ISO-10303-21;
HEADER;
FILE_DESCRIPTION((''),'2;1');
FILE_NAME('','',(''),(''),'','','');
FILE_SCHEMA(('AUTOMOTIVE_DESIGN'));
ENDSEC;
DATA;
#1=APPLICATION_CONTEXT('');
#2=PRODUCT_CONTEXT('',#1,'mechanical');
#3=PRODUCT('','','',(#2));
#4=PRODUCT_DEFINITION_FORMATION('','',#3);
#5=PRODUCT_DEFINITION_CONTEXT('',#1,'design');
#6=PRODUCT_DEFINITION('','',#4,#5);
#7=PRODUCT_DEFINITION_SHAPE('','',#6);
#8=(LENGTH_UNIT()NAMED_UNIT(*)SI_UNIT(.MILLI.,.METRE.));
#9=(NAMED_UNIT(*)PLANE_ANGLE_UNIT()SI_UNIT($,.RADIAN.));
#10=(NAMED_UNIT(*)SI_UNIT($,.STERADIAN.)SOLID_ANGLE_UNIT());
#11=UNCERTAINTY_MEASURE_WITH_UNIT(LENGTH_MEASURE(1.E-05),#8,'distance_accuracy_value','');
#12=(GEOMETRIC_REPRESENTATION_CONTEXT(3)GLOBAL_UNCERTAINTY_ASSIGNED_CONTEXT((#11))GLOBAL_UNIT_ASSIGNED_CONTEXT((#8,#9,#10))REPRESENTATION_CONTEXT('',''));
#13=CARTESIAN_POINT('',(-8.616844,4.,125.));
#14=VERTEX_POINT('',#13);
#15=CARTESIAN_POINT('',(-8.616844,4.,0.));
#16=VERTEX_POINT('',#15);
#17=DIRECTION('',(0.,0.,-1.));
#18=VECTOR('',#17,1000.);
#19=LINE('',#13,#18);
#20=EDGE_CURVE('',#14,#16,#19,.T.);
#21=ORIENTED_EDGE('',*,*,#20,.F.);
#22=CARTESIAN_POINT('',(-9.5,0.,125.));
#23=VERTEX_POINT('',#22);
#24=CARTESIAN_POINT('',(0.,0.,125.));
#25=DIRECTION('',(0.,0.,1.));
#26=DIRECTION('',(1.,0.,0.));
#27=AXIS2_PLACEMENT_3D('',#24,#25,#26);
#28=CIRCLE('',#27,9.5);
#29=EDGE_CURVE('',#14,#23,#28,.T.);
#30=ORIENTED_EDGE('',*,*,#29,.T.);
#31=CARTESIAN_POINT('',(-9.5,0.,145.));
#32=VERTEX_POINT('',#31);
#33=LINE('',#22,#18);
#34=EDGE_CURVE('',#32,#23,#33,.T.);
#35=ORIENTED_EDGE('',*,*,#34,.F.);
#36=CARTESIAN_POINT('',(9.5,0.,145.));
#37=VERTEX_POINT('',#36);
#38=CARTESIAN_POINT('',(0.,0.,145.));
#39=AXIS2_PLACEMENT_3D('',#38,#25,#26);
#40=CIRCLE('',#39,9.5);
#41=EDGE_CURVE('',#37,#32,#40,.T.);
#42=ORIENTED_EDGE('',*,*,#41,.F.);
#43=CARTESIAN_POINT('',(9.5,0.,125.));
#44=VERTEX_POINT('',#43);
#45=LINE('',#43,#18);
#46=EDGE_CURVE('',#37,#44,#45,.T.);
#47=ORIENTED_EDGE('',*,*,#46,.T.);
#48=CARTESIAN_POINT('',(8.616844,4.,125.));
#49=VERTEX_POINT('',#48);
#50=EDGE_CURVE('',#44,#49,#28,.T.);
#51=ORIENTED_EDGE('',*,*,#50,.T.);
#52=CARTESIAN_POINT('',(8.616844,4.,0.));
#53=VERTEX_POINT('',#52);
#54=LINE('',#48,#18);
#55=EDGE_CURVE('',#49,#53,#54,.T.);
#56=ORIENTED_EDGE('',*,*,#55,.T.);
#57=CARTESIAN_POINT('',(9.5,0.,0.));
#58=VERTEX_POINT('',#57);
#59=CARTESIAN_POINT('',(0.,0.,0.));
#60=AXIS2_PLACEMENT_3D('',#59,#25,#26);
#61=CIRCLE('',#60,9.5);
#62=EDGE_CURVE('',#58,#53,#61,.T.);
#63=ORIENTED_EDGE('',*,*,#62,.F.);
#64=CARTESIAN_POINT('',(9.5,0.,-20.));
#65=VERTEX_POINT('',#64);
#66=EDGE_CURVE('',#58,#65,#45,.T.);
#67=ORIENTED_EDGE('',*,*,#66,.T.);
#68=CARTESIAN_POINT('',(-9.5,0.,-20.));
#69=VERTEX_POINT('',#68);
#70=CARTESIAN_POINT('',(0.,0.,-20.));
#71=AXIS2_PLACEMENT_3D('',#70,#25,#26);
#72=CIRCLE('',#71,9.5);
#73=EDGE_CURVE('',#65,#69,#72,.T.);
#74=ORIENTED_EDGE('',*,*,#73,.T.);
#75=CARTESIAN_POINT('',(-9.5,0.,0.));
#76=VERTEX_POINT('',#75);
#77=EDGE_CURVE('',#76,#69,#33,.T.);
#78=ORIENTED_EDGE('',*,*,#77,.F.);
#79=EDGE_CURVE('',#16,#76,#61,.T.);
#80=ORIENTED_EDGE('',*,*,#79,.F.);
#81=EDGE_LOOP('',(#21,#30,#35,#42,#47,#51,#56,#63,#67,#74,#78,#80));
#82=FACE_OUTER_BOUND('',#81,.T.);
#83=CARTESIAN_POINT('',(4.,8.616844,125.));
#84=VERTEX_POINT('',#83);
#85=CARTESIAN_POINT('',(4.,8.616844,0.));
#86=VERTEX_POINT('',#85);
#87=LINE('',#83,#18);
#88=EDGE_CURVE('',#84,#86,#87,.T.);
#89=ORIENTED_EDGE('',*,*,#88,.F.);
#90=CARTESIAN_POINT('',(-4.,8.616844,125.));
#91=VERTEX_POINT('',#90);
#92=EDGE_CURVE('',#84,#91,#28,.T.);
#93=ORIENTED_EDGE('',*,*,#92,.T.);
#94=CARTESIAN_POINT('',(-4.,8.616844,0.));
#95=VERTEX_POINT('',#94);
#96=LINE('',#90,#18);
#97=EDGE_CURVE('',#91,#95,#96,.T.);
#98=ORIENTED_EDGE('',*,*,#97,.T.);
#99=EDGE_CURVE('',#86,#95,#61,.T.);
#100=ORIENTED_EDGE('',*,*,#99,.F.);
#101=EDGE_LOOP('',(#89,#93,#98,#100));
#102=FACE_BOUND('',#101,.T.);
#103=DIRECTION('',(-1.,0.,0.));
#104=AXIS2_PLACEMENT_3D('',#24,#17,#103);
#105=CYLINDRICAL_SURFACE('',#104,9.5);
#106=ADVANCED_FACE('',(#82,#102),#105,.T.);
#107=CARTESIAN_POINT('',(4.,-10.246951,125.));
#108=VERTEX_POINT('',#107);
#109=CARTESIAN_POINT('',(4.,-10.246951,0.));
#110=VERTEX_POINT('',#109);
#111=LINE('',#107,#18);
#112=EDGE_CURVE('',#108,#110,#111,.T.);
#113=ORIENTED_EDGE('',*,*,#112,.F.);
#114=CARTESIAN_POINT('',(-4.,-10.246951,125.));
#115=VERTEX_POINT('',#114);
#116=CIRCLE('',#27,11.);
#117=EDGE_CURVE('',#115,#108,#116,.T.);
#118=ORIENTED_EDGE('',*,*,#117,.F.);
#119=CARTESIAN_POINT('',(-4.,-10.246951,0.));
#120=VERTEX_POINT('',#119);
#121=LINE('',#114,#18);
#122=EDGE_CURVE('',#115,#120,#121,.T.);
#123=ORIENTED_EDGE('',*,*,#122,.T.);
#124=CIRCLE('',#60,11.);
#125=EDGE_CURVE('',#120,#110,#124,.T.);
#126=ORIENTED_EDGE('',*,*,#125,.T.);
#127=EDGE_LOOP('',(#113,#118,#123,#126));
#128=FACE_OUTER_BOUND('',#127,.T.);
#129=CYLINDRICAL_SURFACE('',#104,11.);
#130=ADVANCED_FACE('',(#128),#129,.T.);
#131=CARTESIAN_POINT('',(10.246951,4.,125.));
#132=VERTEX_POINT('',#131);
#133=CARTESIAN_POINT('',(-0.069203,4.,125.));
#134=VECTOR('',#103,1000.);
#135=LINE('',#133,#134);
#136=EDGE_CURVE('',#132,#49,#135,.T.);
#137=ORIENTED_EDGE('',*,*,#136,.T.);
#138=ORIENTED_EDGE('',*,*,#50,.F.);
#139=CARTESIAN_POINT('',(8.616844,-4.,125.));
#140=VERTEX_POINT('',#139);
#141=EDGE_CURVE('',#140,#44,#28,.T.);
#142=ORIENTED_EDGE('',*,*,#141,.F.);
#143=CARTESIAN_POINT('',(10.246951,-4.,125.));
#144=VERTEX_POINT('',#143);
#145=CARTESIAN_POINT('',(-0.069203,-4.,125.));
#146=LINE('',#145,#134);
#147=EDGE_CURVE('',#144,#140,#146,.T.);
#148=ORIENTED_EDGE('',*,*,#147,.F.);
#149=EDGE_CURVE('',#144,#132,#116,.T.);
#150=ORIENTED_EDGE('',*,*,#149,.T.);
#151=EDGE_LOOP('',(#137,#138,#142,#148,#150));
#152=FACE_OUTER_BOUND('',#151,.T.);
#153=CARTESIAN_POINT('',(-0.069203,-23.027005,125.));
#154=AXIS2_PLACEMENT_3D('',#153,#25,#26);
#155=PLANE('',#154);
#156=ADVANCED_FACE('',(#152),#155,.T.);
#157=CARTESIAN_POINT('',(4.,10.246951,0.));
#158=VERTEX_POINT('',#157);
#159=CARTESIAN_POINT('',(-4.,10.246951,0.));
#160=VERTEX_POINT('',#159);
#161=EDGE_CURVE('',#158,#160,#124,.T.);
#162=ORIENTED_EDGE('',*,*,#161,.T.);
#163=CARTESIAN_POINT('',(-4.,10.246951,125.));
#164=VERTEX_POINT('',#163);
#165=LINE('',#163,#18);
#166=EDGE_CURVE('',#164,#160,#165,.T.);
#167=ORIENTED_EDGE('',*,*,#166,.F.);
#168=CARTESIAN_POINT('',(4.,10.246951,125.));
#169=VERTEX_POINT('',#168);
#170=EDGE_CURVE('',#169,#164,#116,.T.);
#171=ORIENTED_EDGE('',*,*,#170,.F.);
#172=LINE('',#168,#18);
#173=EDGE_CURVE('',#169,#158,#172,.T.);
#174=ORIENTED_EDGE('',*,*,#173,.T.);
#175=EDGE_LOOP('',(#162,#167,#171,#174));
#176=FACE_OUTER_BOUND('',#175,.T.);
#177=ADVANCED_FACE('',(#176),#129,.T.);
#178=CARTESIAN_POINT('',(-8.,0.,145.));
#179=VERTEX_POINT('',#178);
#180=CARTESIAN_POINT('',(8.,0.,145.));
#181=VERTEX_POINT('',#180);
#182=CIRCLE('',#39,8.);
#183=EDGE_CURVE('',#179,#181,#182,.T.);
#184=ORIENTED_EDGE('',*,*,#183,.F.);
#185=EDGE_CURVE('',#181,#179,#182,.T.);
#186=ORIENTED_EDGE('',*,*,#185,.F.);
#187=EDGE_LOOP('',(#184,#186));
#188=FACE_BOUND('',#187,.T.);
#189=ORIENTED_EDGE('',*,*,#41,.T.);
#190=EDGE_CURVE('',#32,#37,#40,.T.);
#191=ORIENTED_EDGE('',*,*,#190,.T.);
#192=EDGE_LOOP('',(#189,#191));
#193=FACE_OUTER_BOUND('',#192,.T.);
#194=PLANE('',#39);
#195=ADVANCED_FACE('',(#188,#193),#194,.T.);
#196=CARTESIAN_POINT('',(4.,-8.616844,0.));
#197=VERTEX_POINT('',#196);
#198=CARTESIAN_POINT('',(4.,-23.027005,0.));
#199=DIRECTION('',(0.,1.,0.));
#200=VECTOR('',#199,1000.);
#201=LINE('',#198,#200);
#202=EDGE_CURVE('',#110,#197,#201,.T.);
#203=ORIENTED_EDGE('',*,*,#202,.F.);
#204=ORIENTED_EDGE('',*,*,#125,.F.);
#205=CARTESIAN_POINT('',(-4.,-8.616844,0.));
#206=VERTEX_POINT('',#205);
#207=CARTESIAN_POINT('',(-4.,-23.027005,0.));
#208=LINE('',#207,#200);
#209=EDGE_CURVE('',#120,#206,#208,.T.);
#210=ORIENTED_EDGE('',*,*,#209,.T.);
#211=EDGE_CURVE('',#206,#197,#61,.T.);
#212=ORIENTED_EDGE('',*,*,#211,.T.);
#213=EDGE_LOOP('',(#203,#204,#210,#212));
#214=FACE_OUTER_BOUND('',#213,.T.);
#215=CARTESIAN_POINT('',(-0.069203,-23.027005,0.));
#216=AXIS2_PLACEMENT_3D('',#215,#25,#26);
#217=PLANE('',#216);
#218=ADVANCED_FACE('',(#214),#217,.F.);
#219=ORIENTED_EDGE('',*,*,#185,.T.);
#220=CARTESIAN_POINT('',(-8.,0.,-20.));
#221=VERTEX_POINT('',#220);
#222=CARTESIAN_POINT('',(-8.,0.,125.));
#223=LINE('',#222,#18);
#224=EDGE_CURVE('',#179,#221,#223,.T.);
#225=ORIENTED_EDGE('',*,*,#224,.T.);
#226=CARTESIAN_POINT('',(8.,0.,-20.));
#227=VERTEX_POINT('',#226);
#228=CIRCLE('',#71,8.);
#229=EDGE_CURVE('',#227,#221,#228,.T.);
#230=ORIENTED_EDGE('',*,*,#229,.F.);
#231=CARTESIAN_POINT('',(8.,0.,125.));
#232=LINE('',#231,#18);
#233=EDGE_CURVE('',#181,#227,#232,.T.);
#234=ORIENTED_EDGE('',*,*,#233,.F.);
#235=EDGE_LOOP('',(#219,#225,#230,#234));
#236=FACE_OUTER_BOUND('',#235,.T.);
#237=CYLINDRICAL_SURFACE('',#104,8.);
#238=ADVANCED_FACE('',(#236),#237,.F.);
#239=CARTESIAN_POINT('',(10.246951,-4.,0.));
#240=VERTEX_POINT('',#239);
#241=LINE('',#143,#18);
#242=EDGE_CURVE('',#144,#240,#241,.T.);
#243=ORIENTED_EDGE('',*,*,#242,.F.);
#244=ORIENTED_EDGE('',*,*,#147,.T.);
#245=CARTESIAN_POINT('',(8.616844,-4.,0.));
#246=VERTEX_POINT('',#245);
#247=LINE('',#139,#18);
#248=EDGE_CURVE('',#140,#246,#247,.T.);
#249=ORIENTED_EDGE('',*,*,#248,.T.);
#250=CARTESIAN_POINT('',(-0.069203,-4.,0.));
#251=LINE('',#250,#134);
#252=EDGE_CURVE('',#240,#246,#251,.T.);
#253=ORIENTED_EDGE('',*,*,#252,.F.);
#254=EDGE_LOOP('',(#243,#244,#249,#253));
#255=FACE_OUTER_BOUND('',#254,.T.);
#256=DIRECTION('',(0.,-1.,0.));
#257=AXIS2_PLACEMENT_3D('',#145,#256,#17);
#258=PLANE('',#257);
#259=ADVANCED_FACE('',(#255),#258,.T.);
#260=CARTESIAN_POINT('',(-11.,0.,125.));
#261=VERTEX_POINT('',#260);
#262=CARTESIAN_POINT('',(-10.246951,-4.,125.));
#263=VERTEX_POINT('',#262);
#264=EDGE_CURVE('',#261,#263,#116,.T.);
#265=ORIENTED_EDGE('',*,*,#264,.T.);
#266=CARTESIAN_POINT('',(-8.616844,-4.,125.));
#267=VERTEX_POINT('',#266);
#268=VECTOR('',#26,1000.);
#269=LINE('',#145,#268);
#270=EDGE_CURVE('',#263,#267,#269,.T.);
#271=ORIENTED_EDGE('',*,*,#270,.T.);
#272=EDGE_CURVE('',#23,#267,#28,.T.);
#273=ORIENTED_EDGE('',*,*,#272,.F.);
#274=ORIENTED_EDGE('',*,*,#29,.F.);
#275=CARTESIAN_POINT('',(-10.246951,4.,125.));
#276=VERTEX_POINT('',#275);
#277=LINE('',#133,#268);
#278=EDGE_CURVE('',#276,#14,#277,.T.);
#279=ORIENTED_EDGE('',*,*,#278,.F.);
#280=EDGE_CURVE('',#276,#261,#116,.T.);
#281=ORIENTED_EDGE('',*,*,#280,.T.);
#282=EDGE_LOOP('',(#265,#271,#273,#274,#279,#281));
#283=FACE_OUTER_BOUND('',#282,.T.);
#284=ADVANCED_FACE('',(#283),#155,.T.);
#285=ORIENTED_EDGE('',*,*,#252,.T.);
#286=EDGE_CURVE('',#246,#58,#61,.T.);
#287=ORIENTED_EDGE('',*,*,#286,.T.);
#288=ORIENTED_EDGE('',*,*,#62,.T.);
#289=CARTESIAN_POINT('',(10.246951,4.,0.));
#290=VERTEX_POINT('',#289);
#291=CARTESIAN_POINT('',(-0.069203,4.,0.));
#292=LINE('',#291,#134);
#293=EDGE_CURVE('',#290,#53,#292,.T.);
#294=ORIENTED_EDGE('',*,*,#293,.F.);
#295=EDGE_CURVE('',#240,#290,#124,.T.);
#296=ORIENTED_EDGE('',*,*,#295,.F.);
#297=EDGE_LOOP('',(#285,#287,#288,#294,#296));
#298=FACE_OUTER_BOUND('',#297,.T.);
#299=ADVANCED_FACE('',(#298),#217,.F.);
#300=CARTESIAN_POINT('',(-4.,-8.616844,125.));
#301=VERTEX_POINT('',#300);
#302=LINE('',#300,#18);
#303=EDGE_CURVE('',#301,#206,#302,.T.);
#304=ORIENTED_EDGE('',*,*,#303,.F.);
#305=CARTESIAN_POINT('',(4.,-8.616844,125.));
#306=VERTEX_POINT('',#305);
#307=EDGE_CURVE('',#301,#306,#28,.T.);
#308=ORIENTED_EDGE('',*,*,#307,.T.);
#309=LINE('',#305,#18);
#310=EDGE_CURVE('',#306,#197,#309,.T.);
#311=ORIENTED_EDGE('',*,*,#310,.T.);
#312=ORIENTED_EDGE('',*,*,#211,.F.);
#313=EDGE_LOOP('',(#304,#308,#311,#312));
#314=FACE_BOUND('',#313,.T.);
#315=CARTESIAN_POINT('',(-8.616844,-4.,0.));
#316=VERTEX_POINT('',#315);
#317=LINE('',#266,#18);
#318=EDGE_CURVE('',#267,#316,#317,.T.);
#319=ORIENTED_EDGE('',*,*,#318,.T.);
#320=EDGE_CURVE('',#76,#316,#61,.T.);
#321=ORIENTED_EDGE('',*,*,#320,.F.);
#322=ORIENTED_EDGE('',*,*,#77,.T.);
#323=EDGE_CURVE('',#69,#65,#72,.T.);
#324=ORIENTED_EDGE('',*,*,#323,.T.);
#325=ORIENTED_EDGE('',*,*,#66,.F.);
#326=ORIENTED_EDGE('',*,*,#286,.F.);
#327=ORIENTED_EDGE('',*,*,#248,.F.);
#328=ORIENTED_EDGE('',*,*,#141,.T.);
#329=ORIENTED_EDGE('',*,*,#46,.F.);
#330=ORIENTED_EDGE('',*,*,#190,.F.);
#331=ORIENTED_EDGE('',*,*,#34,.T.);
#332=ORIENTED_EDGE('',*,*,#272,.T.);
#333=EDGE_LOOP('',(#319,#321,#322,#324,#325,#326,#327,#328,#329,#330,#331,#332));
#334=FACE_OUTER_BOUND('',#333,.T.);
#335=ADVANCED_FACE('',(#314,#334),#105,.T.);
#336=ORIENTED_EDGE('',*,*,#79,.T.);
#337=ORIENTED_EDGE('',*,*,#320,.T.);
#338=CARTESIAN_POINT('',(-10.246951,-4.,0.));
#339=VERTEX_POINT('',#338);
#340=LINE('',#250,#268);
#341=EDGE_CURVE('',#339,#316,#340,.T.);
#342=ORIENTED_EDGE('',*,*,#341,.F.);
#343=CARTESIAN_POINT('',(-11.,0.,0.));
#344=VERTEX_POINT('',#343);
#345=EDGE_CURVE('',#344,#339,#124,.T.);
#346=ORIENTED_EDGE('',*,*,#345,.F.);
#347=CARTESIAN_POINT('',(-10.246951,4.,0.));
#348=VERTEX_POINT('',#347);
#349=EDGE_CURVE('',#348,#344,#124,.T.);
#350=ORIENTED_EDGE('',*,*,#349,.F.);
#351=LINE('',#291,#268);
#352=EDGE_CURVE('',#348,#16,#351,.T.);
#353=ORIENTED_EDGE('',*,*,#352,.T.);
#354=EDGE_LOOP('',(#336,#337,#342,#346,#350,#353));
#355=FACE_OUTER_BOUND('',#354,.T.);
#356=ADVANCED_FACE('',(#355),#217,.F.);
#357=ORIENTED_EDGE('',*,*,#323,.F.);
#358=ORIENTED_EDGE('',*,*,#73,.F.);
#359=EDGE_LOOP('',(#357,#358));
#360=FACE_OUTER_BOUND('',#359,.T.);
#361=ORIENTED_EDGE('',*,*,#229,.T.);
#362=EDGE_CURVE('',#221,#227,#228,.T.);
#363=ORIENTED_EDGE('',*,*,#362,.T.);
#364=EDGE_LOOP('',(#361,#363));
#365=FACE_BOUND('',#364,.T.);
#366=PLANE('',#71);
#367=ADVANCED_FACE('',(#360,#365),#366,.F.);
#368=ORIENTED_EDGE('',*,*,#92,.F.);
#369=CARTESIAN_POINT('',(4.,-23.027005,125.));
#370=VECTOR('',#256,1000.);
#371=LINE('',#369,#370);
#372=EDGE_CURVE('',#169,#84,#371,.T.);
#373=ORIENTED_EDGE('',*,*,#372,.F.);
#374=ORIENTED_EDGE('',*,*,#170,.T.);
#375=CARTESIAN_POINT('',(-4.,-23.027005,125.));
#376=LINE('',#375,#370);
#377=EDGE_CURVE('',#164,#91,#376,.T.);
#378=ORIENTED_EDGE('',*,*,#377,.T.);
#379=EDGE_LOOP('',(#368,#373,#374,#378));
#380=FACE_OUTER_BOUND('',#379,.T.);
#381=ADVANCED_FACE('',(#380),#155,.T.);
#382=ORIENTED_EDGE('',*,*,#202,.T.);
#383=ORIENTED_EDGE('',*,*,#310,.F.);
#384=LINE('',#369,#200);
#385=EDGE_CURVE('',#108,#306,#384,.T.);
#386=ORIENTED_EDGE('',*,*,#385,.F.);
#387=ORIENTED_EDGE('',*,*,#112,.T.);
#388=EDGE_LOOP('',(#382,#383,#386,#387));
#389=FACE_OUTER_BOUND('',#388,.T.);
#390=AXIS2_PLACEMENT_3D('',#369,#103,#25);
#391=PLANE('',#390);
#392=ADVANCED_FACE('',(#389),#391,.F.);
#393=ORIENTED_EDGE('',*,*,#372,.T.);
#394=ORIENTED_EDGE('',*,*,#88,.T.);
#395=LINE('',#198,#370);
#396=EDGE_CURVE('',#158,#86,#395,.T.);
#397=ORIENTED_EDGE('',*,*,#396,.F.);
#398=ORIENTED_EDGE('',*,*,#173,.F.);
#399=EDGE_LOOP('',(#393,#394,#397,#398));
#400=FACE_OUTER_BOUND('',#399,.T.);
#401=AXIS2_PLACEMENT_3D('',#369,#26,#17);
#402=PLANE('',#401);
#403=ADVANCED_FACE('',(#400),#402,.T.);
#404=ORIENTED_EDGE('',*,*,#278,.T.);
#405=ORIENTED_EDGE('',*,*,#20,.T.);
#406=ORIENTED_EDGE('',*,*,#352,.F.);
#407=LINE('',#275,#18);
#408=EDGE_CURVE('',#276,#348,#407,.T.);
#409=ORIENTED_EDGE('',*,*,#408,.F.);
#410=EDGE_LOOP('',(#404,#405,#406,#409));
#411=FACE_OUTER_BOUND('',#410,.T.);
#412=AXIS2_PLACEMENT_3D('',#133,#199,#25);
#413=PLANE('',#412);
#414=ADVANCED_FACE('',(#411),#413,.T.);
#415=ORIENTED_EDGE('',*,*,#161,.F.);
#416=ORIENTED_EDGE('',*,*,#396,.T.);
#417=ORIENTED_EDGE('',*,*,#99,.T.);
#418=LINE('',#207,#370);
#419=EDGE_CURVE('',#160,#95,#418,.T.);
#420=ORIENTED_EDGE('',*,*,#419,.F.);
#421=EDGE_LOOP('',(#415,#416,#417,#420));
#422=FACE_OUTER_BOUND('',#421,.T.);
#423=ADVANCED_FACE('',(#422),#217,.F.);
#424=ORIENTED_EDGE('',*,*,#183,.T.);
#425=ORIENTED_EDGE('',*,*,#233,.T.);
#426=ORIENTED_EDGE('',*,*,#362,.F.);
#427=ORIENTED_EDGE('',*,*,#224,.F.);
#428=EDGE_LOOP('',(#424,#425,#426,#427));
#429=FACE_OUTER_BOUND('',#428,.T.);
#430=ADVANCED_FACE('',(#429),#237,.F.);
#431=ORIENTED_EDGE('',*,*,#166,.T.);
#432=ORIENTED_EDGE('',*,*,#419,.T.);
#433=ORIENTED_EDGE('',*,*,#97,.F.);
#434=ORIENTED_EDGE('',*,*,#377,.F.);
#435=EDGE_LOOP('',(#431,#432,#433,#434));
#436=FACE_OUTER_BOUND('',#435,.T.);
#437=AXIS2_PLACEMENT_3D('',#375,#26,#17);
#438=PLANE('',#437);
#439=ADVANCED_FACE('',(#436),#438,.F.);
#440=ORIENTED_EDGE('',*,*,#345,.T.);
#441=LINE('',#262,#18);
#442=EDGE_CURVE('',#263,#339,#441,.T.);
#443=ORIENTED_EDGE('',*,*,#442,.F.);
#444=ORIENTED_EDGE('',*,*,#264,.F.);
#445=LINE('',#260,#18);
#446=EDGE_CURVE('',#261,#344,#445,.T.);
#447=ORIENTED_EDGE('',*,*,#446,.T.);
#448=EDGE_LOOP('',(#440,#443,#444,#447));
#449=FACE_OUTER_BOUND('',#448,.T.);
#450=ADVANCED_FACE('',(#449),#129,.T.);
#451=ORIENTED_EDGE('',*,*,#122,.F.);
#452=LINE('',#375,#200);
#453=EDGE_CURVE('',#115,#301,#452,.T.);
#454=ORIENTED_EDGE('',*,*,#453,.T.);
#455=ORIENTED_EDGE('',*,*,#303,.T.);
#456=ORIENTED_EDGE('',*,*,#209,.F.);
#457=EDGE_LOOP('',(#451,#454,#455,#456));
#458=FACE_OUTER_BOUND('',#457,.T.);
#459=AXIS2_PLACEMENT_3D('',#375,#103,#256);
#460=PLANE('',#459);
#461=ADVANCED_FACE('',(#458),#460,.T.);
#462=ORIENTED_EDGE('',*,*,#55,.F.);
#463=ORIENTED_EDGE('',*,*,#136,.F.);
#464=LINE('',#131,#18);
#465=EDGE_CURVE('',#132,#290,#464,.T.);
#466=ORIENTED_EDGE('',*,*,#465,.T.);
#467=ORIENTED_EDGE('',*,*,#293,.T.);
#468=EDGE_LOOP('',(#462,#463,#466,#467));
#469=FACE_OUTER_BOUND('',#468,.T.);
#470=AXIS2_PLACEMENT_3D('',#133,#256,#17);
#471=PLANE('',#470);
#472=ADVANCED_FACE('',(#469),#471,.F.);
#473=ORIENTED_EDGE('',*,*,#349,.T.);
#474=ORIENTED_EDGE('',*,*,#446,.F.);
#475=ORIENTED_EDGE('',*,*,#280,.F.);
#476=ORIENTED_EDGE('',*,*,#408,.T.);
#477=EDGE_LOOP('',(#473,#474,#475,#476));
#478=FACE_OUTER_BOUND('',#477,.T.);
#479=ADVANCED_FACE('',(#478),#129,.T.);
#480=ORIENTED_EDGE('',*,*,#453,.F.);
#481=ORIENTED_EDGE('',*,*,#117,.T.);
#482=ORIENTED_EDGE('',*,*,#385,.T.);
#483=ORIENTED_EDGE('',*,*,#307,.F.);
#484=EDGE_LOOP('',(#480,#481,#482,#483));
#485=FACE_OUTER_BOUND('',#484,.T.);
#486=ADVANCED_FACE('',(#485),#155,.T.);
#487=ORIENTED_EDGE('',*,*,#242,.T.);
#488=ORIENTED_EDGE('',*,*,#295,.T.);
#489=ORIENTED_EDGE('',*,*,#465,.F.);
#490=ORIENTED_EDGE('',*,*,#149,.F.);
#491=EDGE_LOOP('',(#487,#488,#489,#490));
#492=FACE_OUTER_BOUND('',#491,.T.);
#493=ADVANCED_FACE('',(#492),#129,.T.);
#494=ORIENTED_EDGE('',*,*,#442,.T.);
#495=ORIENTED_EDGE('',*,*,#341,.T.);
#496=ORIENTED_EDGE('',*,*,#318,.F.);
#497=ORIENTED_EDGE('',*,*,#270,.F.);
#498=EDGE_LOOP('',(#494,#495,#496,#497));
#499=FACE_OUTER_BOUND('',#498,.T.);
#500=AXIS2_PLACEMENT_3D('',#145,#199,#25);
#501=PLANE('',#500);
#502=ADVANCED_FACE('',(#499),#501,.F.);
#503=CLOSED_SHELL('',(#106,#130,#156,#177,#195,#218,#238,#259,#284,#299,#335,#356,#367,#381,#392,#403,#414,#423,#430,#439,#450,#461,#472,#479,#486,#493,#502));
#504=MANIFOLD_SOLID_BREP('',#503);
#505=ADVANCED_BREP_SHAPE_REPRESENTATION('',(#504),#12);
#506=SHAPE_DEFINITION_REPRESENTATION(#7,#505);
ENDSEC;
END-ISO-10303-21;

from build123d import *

# Parameters (mm, degrees)
EXTRUDE_1_DEPTH      = 125
EXTRUDE_2_DEPTH      = 20
EXTRUDE_2_DEPTH_BACK = 145
SKETCH_2_R           = 9.5
SKETCH_2_R_2         = 8


with BuildPart() as part:
    # 草图1 → 凸台-拉伸1 (new body)
    with BuildSketch(Plane.XY):
        with BuildLine():
            Line((-4, 10.246950766), (-4, 8.61684397))
            ThreePointArc((-4, 8.61684397), (-6.717514421, 6.717514421), (-8.61684397, 4))
            Line((-8.61684397, 4), (-10.246950766, 4))
            ThreePointArc((-10.246950766, 4), (-11, 0), (-10.246950766, -4))
            Line((-10.246950766, -4), (-8.61684397, -4))
            ThreePointArc((-8.61684397, -4), (-6.717514421, -6.717514421), (-4, -8.61684397))
            Line((-4, -8.61684397), (-4, -10.246950766))
            ThreePointArc((-4, -10.246950766), (0, -11), (4, -10.246950766))
            Line((4, -10.246950766), (4, -8.61684397))
            ThreePointArc((4, -8.61684397), (6.717514421, -6.717514421), (8.61684397, -4))
            Line((8.61684397, -4), (10.246950766, -4))
            ThreePointArc((10.246950766, -4), (11, 0), (10.246950766, 4))
            Line((10.246950766, 4), (8.61684397, 4))
            ThreePointArc((8.61684397, 4), (6.717514421, 6.717514421), (4, 8.61684397))
            Line((4, 8.61684397), (4, 10.246950766))
            ThreePointArc((4, 10.246950766), (0, 11), (-4, 10.246950766))
        make_face()
        with BuildLine():
            Line((-2.5, 9.16515139), (-2.5, 7.599342077))
            ThreePointArc((-2.5, 7.599342077), (-5.656854249, 5.656854249), (-7.599342077, 2.5))
            Line((-7.599342077, 2.5), (-9.16515139, 2.5))
            ThreePointArc((-9.16515139, 2.5), (-9.5, 0), (-9.16515139, -2.5))
            Line((-9.16515139, -2.5), (-7.599342077, -2.5))
            ThreePointArc((-7.599342077, -2.5), (-5.656854249, -5.656854249), (-2.5, -7.599342077))
            Line((-2.5, -7.599342077), (-2.5, -9.16515139))
            ThreePointArc((-2.5, -9.16515139), (0, -9.5), (2.5, -9.16515139))
            Line((2.5, -9.16515139), (2.5, -7.599342077))
            ThreePointArc((2.5, -7.599342077), (5.656854249, -5.656854249), (7.599342077, -2.5))
            Line((7.599342077, -2.5), (9.16515139, -2.5))
            ThreePointArc((9.16515139, -2.5), (9.5, 0), (9.16515139, 2.5))
            Line((9.16515139, 2.5), (7.599342077, 2.5))
            ThreePointArc((7.599342077, 2.5), (5.656854249, 5.656854249), (2.5, 7.599342077))
            Line((2.5, 7.599342077), (2.5, 9.16515139))
            ThreePointArc((2.5, 9.16515139), (0, 9.5), (-2.5, 9.16515139))
        make_face(mode=Mode.SUBTRACT)
    extrude(amount=EXTRUDE_1_DEPTH)

    # 草图2 → 凸台-拉伸2 (add, two sides: drawn at the far end of the back side and taken through both)
    with BuildSketch(Plane.XY.offset(125).offset(-EXTRUDE_2_DEPTH_BACK)):
        Circle(SKETCH_2_R)
        Circle(SKETCH_2_R_2, mode=Mode.SUBTRACT)
    extrude(amount=EXTRUDE_2_DEPTH + EXTRUDE_2_DEPTH_BACK)


solid = part.part
